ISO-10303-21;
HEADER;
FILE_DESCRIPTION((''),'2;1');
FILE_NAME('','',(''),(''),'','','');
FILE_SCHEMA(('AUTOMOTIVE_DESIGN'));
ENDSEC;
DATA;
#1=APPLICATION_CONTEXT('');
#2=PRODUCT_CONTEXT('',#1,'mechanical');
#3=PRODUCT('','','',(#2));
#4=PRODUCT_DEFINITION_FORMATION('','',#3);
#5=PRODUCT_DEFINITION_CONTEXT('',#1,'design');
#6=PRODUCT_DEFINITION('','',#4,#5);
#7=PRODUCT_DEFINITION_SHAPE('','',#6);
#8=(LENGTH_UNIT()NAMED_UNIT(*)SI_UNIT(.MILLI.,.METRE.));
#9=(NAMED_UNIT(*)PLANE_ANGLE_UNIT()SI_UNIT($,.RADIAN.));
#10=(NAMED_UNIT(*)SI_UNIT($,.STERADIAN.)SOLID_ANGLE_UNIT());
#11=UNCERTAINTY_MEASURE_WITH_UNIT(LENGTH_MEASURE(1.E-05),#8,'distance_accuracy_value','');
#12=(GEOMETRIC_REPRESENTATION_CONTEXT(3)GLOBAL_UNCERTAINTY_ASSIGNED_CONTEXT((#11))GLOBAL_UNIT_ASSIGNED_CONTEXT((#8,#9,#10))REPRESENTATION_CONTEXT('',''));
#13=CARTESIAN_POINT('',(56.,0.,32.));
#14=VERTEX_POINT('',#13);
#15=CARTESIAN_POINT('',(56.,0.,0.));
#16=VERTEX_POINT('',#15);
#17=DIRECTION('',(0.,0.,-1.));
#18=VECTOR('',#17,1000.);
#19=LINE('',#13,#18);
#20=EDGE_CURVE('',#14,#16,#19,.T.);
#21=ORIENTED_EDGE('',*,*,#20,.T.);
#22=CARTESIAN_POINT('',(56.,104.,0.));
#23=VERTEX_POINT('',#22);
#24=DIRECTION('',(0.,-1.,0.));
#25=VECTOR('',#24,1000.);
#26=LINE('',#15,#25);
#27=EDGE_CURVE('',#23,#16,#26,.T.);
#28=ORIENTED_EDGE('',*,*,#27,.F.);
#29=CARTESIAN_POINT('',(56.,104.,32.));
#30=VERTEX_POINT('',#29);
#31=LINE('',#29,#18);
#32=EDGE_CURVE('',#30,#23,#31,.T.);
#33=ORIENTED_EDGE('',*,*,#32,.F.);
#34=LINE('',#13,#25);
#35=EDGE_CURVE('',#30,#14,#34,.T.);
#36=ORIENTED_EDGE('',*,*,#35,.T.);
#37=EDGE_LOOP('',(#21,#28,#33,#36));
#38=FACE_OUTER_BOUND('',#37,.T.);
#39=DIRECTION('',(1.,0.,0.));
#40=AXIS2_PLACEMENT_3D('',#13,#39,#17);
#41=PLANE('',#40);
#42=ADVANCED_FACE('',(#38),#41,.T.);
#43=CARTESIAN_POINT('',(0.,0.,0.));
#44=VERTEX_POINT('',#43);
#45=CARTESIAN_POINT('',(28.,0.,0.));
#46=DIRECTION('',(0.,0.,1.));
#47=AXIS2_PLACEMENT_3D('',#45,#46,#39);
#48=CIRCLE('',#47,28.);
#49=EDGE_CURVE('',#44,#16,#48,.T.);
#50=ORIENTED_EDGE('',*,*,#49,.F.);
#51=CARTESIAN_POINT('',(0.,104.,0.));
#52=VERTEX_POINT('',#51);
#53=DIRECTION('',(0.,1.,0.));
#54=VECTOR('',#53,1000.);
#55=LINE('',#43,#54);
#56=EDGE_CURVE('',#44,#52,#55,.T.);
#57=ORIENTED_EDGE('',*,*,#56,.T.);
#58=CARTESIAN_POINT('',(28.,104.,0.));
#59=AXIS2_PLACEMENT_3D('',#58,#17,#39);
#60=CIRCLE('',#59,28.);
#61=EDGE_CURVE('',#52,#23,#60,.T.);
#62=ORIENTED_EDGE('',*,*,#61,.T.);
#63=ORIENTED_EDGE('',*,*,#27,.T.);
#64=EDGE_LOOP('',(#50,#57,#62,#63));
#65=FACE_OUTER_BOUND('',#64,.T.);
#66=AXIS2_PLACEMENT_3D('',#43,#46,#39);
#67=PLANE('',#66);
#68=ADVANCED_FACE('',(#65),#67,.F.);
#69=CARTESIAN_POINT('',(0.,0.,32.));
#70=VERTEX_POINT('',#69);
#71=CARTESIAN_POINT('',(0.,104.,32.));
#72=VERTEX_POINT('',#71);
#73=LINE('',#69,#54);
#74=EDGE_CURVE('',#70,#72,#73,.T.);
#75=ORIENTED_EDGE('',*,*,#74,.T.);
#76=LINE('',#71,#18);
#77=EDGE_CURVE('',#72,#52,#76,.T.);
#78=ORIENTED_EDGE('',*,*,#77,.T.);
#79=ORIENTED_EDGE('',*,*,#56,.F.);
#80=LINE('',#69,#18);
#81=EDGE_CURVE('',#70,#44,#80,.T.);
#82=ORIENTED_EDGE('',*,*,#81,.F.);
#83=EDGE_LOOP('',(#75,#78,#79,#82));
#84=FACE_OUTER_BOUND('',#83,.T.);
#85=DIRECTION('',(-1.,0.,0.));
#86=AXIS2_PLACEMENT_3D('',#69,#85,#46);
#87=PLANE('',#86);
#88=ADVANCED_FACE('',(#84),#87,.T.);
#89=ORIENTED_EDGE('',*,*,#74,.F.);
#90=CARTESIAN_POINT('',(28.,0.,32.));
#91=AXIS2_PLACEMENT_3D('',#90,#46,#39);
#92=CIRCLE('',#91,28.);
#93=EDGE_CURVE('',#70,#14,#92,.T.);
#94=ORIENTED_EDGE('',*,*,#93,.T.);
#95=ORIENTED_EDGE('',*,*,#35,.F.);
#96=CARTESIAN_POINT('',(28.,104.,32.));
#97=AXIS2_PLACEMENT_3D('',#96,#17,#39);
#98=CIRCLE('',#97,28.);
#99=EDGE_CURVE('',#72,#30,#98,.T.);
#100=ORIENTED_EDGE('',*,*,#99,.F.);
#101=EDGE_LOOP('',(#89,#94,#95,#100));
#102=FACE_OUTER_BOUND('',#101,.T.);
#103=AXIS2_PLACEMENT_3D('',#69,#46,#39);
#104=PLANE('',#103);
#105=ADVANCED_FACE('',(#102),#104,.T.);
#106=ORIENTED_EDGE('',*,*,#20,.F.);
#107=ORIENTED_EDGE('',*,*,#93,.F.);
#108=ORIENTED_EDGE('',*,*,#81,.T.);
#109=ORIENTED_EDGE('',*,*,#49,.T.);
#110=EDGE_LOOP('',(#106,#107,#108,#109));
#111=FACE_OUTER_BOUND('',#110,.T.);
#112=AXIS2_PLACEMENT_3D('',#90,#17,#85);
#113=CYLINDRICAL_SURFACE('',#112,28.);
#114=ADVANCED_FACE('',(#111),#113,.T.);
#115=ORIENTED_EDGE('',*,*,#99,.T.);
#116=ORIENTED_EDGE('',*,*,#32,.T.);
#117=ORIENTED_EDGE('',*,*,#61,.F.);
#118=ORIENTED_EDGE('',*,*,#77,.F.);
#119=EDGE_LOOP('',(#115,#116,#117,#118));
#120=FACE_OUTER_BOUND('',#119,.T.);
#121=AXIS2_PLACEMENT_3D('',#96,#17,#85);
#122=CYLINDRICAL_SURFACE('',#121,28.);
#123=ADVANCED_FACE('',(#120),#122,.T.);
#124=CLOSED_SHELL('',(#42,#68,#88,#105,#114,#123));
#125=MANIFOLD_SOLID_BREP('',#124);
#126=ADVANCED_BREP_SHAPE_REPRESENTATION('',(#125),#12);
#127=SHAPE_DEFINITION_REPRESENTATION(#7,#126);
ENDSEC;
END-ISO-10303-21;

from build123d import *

# Parameters (mm, degrees)
EXTRUDE_1_DEPTH = 32


with BuildPart() as part:
    # 草图1 → 凸台-拉伸1 (new body)
    with BuildSketch(Plane.XY):
        with BuildLine():
            Line((0, 0), (0, 104))
            ThreePointArc((0, 104), (28, 132), (56, 104))
            Line((56, 104), (56, 0))
            ThreePointArc((56, 0), (28, -28), (0, 0))
        make_face()
    extrude(amount=EXTRUDE_1_DEPTH)


solid = part.part
